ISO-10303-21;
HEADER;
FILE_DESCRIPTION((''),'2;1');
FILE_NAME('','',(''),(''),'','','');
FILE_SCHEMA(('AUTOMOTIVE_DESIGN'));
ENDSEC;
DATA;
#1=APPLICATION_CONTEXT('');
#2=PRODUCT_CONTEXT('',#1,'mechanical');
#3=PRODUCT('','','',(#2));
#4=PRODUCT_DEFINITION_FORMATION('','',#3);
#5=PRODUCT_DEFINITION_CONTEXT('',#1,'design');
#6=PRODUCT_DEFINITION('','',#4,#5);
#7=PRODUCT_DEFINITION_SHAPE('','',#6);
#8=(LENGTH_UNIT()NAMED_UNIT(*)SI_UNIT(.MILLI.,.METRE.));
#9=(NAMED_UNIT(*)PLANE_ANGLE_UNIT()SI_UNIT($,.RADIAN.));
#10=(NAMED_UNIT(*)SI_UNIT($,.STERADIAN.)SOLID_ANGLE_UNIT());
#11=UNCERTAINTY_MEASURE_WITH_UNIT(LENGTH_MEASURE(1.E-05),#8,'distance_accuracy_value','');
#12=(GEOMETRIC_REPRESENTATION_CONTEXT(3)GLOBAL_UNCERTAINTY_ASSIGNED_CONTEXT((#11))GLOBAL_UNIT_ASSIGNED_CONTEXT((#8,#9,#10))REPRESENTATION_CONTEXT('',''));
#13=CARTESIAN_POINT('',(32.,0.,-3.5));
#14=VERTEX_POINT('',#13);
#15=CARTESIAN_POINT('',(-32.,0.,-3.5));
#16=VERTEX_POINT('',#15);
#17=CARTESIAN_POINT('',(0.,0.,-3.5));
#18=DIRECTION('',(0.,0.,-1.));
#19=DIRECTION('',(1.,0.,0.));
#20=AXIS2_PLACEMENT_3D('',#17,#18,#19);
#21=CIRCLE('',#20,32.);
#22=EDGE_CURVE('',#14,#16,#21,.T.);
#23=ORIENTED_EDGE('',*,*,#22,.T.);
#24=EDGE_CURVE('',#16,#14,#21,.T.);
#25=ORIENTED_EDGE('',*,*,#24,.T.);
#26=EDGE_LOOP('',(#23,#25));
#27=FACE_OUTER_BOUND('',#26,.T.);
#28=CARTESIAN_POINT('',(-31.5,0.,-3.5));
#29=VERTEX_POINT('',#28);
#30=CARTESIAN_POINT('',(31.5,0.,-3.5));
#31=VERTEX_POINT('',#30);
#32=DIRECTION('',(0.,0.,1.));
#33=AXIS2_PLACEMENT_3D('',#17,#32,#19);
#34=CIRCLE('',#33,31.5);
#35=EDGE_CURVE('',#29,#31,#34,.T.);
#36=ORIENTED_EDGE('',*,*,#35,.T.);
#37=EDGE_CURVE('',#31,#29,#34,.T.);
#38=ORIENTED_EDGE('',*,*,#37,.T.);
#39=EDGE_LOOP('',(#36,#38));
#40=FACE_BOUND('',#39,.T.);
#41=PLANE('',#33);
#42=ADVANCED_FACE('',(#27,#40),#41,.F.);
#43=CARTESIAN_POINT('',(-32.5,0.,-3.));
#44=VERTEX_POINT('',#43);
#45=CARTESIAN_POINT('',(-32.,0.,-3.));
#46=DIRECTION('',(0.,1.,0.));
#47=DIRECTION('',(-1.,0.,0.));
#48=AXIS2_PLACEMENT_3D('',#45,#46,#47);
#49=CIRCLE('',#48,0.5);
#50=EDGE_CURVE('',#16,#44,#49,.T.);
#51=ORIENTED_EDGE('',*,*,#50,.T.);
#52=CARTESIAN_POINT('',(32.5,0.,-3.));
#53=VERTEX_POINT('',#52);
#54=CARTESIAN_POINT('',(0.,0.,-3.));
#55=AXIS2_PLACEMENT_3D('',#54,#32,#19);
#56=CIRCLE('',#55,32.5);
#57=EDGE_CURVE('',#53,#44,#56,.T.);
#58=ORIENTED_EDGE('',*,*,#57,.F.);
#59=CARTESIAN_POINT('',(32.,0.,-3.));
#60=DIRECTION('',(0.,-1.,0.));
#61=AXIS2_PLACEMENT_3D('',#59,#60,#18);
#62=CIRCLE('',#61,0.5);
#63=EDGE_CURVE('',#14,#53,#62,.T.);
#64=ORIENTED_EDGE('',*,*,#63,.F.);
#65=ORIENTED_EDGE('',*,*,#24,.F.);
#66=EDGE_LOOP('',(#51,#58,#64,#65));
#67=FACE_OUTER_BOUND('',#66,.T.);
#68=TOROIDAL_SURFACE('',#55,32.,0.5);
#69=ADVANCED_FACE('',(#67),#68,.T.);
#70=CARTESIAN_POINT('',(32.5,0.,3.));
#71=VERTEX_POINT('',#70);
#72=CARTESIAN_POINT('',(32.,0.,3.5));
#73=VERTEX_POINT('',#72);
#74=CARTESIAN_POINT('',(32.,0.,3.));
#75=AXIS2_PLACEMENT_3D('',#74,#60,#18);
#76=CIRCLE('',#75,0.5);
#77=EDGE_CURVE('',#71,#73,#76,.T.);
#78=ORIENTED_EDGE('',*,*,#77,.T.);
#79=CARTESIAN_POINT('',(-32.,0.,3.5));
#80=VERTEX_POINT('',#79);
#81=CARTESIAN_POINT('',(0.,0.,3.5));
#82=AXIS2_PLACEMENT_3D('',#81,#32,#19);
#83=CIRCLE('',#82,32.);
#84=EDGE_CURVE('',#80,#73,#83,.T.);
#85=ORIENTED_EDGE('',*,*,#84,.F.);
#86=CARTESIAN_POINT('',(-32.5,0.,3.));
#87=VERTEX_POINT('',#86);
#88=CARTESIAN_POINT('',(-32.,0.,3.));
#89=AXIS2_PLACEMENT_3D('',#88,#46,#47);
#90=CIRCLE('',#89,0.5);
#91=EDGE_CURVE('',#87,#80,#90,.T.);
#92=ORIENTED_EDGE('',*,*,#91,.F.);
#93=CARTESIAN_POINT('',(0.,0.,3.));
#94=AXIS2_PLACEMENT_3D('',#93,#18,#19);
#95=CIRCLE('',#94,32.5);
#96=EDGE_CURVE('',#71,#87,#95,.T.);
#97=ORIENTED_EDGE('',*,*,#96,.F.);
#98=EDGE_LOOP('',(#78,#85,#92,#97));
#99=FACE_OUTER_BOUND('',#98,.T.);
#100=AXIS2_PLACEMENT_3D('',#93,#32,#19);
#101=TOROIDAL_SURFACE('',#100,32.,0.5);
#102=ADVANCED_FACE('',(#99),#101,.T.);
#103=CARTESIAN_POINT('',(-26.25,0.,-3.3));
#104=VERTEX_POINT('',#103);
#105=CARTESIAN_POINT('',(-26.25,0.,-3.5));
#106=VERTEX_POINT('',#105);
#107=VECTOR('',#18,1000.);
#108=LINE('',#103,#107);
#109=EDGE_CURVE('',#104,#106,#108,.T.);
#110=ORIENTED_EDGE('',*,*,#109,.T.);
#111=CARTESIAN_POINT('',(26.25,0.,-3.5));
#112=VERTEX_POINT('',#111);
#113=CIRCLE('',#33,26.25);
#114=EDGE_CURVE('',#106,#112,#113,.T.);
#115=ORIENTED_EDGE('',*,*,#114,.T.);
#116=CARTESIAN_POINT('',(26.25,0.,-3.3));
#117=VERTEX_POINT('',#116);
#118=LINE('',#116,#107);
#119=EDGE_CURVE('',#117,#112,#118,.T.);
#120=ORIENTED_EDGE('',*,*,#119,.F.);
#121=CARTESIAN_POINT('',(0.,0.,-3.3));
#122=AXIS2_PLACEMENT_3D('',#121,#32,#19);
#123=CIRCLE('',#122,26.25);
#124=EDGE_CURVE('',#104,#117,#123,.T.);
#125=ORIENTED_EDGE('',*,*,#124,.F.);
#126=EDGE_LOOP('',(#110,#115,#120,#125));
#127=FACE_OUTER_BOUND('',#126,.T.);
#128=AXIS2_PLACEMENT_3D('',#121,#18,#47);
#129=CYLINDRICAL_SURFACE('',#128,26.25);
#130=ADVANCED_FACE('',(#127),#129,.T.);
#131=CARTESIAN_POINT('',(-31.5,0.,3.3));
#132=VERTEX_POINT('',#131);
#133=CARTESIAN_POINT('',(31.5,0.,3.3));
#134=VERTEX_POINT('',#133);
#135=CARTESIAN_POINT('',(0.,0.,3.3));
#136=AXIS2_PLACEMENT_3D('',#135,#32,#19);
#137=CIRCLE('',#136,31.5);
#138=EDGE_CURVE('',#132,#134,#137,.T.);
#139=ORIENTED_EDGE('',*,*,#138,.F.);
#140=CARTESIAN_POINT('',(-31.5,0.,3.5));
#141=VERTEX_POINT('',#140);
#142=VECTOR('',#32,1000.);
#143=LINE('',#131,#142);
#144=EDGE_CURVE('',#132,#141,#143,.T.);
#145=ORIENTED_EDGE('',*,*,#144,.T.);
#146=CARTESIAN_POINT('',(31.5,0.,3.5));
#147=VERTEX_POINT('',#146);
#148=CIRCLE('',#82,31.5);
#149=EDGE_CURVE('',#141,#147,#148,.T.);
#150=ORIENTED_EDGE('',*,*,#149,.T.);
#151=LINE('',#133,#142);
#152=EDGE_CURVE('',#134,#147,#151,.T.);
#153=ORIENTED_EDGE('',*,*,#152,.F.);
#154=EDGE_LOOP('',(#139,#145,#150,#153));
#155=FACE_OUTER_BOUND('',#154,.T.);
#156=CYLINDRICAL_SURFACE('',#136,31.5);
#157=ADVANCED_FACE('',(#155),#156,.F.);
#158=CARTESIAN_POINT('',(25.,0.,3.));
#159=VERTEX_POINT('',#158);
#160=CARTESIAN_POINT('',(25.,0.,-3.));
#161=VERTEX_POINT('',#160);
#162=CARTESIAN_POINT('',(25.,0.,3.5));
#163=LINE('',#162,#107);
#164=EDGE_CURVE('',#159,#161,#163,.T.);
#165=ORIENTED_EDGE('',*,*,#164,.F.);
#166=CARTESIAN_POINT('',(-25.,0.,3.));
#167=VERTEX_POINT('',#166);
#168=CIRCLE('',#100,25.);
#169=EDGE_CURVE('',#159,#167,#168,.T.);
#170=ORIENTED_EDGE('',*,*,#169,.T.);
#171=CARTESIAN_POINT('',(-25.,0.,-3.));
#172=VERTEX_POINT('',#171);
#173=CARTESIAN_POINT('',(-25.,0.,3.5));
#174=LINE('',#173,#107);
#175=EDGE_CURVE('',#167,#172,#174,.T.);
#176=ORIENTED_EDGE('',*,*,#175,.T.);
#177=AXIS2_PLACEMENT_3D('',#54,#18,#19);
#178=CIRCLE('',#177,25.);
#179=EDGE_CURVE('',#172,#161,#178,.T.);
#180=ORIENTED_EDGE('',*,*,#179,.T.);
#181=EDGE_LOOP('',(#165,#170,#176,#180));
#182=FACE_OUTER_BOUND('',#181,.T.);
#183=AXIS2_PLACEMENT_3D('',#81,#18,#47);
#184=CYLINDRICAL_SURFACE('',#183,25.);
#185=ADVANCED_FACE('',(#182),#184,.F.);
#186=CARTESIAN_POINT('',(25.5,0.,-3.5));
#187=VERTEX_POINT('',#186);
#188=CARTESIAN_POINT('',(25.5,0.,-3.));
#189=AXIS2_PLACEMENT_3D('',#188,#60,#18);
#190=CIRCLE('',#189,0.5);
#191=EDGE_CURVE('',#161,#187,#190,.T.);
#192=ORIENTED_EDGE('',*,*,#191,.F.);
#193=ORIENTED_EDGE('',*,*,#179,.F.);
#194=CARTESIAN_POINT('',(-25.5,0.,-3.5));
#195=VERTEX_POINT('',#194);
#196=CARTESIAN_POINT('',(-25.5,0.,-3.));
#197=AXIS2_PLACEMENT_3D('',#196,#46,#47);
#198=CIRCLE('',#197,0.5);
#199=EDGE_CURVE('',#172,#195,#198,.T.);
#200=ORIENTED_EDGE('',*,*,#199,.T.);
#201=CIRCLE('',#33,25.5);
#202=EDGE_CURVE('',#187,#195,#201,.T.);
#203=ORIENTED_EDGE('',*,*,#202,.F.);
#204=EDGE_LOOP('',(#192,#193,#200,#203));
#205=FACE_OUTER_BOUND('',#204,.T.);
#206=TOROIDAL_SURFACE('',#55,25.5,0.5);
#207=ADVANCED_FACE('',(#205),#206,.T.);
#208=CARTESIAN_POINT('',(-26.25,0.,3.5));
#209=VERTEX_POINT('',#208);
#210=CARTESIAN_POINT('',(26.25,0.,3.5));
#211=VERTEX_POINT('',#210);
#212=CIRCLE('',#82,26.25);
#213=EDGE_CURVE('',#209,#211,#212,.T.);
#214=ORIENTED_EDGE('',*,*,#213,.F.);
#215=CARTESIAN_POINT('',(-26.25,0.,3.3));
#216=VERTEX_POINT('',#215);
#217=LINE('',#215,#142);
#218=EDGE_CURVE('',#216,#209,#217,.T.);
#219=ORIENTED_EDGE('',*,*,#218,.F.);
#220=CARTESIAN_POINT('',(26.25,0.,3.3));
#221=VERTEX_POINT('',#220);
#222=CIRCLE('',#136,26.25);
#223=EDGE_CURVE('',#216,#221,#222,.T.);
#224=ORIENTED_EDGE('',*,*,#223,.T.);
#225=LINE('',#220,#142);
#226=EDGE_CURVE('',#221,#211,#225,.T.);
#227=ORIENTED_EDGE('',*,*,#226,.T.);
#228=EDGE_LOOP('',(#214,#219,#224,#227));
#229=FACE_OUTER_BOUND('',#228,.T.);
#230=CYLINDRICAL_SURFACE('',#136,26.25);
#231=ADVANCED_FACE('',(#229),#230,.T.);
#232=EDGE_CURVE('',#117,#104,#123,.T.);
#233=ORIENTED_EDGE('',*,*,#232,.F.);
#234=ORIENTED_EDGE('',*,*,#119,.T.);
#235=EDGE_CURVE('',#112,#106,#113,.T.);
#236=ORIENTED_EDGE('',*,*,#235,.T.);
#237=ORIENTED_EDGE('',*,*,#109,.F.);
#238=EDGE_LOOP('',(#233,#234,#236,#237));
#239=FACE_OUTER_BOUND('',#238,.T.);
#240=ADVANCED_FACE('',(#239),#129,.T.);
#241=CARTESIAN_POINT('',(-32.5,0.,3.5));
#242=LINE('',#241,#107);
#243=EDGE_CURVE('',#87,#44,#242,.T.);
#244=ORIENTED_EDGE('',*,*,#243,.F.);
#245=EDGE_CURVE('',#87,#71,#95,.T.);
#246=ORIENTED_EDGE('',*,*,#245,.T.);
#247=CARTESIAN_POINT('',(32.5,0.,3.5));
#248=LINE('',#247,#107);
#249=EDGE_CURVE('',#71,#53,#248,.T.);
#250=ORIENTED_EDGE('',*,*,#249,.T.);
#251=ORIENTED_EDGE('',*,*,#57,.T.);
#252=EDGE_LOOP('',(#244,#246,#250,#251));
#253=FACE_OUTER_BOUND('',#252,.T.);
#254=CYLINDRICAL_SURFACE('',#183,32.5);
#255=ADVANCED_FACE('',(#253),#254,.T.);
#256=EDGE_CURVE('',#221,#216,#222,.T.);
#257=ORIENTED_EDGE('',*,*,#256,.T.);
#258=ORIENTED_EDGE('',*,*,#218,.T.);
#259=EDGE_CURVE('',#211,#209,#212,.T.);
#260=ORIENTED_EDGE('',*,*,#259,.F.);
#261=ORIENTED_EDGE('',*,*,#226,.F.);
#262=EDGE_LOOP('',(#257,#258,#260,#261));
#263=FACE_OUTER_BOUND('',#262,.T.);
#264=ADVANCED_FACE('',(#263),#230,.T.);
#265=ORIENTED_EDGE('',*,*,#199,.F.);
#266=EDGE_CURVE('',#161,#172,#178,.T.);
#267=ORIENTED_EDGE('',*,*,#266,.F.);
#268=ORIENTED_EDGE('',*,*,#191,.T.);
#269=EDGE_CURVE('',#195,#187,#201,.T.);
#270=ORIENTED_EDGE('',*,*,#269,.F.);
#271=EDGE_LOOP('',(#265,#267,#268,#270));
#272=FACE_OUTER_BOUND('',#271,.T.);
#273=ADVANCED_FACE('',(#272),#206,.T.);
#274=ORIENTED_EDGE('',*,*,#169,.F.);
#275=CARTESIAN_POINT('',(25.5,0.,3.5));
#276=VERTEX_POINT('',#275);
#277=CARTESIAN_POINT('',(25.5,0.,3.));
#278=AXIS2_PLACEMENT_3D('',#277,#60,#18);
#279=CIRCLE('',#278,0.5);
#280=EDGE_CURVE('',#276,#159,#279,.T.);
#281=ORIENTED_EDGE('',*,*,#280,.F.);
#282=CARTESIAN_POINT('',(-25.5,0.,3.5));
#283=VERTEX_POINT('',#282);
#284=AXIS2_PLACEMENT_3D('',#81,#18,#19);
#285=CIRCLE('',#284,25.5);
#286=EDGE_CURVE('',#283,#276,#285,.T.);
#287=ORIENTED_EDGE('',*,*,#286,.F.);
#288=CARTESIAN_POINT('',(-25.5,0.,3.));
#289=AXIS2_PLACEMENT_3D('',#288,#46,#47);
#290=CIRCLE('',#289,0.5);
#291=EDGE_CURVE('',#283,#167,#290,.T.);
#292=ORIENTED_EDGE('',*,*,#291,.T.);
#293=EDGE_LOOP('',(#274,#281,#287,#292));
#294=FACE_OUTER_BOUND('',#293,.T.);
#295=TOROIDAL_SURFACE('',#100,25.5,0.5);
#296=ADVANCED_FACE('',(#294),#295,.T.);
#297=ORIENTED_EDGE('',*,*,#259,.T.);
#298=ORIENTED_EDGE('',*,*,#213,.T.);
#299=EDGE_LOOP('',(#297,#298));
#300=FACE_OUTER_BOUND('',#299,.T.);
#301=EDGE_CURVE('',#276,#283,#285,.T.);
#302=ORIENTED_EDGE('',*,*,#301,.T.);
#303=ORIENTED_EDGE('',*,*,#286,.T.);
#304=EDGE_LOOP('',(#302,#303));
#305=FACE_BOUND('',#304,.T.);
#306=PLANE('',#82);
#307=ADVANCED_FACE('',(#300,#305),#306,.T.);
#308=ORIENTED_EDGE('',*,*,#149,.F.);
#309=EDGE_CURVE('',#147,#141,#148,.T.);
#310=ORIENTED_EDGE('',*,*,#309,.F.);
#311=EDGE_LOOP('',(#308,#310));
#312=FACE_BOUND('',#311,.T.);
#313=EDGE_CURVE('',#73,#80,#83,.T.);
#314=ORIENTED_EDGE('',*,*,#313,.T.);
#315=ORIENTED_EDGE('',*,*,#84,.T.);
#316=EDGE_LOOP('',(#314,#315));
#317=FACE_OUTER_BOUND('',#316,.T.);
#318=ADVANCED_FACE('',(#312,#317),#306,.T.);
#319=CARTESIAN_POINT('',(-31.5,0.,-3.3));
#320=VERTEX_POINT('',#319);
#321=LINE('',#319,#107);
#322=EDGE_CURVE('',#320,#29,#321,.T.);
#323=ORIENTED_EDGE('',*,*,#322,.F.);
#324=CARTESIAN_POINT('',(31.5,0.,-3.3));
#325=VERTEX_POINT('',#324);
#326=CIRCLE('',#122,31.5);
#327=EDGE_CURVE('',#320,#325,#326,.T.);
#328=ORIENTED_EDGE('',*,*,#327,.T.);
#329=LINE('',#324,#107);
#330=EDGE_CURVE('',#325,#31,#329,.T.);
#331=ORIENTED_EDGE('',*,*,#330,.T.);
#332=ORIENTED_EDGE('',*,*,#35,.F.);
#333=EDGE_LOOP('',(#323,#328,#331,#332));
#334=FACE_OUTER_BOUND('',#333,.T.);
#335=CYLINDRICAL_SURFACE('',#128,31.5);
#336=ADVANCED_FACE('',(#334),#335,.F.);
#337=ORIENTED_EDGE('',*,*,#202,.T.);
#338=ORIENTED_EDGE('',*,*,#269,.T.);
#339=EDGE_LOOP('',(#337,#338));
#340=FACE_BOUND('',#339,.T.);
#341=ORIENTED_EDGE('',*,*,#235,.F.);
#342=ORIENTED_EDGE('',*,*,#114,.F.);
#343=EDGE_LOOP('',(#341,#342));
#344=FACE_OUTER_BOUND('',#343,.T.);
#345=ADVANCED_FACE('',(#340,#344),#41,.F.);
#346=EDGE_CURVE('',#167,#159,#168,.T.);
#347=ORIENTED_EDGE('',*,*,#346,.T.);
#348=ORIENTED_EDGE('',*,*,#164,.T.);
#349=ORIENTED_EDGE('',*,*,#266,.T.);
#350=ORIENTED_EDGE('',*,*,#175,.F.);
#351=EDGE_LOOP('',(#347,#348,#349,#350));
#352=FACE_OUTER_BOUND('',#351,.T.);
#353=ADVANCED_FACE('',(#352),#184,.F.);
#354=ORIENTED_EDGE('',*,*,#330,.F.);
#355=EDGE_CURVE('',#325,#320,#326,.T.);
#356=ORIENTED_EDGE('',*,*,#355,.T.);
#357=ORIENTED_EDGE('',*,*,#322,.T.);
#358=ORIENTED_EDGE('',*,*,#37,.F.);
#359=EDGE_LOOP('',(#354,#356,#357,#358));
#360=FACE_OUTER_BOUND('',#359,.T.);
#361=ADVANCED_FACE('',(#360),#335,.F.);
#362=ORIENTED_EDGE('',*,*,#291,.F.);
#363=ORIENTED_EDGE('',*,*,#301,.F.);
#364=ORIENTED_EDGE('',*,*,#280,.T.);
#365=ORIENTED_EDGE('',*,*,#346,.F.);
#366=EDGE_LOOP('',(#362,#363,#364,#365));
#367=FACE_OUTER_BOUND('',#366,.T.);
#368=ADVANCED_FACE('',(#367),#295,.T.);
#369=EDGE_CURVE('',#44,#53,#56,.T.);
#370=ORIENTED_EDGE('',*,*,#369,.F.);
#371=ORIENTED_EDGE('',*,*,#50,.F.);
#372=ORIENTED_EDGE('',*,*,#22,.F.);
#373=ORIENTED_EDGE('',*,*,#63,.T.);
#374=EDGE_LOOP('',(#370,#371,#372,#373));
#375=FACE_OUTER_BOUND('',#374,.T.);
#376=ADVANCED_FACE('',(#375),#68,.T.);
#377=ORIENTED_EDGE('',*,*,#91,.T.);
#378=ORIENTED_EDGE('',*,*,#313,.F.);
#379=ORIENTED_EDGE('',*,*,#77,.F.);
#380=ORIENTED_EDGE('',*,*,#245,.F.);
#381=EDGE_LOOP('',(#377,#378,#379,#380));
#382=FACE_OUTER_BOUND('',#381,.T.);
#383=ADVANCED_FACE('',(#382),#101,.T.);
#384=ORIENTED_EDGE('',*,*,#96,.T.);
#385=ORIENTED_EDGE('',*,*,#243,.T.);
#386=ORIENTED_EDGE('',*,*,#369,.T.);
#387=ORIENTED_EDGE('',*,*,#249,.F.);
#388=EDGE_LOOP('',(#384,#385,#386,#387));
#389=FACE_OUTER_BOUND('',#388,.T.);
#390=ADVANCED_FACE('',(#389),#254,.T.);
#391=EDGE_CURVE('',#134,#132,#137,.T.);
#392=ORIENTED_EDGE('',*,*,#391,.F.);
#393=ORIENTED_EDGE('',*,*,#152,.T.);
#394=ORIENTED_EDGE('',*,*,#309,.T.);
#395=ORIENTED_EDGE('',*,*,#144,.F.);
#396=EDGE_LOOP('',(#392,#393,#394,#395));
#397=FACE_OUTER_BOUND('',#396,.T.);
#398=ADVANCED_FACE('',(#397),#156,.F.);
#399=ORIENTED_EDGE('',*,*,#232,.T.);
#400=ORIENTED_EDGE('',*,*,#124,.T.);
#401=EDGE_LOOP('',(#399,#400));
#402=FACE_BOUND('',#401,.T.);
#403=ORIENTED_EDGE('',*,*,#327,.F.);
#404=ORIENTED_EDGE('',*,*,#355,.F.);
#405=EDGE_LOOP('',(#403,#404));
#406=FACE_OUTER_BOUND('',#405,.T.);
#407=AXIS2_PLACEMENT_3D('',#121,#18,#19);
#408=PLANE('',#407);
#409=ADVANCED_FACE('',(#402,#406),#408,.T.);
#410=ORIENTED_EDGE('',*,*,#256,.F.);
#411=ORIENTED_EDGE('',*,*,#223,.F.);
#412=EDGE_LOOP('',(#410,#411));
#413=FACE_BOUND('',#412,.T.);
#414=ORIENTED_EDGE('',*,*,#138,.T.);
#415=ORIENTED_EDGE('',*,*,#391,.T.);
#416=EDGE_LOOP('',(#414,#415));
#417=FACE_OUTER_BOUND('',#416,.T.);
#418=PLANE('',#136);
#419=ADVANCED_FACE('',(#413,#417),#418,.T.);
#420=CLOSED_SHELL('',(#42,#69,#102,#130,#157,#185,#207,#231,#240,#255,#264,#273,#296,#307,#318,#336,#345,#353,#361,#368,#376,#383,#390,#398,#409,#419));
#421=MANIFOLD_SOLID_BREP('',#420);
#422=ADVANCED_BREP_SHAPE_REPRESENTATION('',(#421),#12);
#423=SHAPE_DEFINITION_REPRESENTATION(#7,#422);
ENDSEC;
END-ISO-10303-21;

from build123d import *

# Parameters (mm, degrees)
SKETCH1_R           = 32.5
SKETCH1_R_2         = 25
BOSS_EXTRUDE1_DEPTH = 3.5
SKETCH2_R           = 31.5
SKETCH2_R_2         = 26.25
CUT_EXTRUDE1_DEPTH  = 0.2
FILLET1_R           = 0.5


with BuildPart() as part:
    # Sketch1 → Boss-Extrude1 (new, symmetric)
    with BuildSketch(Plane.XY):
        Circle(SKETCH1_R)
        Circle(SKETCH1_R_2, mode=Mode.SUBTRACT)
    extrude(amount=BOSS_EXTRUDE1_DEPTH, both=True)

    # Sketch2 → Cut-Extrude1 (cut)
    with BuildSketch(Plane.XY.offset(3.5)):
        Circle(SKETCH2_R)
        Circle(SKETCH2_R_2, mode=Mode.SUBTRACT)
    cut_extrude1 = extrude(amount=-CUT_EXTRUDE1_DEPTH, mode=Mode.SUBTRACT)

    # Mirror1: Cut-Extrude1 across plane
    add(cut_extrude1.mirror(Plane.XY), mode=Mode.SUBTRACT)

    # Fillet1
    fillet1_edges = [part.edges().sort_by_distance(p)[0] for p in [
        (-32.5, 0, -3.5),
        (-32.5, 0, 3.5),
        (-25, 0, -3.5),
        (-25, 0, 3.5),
    ]]
    fillet(fillet1_edges, radius=FILLET1_R)


solid = part.part
